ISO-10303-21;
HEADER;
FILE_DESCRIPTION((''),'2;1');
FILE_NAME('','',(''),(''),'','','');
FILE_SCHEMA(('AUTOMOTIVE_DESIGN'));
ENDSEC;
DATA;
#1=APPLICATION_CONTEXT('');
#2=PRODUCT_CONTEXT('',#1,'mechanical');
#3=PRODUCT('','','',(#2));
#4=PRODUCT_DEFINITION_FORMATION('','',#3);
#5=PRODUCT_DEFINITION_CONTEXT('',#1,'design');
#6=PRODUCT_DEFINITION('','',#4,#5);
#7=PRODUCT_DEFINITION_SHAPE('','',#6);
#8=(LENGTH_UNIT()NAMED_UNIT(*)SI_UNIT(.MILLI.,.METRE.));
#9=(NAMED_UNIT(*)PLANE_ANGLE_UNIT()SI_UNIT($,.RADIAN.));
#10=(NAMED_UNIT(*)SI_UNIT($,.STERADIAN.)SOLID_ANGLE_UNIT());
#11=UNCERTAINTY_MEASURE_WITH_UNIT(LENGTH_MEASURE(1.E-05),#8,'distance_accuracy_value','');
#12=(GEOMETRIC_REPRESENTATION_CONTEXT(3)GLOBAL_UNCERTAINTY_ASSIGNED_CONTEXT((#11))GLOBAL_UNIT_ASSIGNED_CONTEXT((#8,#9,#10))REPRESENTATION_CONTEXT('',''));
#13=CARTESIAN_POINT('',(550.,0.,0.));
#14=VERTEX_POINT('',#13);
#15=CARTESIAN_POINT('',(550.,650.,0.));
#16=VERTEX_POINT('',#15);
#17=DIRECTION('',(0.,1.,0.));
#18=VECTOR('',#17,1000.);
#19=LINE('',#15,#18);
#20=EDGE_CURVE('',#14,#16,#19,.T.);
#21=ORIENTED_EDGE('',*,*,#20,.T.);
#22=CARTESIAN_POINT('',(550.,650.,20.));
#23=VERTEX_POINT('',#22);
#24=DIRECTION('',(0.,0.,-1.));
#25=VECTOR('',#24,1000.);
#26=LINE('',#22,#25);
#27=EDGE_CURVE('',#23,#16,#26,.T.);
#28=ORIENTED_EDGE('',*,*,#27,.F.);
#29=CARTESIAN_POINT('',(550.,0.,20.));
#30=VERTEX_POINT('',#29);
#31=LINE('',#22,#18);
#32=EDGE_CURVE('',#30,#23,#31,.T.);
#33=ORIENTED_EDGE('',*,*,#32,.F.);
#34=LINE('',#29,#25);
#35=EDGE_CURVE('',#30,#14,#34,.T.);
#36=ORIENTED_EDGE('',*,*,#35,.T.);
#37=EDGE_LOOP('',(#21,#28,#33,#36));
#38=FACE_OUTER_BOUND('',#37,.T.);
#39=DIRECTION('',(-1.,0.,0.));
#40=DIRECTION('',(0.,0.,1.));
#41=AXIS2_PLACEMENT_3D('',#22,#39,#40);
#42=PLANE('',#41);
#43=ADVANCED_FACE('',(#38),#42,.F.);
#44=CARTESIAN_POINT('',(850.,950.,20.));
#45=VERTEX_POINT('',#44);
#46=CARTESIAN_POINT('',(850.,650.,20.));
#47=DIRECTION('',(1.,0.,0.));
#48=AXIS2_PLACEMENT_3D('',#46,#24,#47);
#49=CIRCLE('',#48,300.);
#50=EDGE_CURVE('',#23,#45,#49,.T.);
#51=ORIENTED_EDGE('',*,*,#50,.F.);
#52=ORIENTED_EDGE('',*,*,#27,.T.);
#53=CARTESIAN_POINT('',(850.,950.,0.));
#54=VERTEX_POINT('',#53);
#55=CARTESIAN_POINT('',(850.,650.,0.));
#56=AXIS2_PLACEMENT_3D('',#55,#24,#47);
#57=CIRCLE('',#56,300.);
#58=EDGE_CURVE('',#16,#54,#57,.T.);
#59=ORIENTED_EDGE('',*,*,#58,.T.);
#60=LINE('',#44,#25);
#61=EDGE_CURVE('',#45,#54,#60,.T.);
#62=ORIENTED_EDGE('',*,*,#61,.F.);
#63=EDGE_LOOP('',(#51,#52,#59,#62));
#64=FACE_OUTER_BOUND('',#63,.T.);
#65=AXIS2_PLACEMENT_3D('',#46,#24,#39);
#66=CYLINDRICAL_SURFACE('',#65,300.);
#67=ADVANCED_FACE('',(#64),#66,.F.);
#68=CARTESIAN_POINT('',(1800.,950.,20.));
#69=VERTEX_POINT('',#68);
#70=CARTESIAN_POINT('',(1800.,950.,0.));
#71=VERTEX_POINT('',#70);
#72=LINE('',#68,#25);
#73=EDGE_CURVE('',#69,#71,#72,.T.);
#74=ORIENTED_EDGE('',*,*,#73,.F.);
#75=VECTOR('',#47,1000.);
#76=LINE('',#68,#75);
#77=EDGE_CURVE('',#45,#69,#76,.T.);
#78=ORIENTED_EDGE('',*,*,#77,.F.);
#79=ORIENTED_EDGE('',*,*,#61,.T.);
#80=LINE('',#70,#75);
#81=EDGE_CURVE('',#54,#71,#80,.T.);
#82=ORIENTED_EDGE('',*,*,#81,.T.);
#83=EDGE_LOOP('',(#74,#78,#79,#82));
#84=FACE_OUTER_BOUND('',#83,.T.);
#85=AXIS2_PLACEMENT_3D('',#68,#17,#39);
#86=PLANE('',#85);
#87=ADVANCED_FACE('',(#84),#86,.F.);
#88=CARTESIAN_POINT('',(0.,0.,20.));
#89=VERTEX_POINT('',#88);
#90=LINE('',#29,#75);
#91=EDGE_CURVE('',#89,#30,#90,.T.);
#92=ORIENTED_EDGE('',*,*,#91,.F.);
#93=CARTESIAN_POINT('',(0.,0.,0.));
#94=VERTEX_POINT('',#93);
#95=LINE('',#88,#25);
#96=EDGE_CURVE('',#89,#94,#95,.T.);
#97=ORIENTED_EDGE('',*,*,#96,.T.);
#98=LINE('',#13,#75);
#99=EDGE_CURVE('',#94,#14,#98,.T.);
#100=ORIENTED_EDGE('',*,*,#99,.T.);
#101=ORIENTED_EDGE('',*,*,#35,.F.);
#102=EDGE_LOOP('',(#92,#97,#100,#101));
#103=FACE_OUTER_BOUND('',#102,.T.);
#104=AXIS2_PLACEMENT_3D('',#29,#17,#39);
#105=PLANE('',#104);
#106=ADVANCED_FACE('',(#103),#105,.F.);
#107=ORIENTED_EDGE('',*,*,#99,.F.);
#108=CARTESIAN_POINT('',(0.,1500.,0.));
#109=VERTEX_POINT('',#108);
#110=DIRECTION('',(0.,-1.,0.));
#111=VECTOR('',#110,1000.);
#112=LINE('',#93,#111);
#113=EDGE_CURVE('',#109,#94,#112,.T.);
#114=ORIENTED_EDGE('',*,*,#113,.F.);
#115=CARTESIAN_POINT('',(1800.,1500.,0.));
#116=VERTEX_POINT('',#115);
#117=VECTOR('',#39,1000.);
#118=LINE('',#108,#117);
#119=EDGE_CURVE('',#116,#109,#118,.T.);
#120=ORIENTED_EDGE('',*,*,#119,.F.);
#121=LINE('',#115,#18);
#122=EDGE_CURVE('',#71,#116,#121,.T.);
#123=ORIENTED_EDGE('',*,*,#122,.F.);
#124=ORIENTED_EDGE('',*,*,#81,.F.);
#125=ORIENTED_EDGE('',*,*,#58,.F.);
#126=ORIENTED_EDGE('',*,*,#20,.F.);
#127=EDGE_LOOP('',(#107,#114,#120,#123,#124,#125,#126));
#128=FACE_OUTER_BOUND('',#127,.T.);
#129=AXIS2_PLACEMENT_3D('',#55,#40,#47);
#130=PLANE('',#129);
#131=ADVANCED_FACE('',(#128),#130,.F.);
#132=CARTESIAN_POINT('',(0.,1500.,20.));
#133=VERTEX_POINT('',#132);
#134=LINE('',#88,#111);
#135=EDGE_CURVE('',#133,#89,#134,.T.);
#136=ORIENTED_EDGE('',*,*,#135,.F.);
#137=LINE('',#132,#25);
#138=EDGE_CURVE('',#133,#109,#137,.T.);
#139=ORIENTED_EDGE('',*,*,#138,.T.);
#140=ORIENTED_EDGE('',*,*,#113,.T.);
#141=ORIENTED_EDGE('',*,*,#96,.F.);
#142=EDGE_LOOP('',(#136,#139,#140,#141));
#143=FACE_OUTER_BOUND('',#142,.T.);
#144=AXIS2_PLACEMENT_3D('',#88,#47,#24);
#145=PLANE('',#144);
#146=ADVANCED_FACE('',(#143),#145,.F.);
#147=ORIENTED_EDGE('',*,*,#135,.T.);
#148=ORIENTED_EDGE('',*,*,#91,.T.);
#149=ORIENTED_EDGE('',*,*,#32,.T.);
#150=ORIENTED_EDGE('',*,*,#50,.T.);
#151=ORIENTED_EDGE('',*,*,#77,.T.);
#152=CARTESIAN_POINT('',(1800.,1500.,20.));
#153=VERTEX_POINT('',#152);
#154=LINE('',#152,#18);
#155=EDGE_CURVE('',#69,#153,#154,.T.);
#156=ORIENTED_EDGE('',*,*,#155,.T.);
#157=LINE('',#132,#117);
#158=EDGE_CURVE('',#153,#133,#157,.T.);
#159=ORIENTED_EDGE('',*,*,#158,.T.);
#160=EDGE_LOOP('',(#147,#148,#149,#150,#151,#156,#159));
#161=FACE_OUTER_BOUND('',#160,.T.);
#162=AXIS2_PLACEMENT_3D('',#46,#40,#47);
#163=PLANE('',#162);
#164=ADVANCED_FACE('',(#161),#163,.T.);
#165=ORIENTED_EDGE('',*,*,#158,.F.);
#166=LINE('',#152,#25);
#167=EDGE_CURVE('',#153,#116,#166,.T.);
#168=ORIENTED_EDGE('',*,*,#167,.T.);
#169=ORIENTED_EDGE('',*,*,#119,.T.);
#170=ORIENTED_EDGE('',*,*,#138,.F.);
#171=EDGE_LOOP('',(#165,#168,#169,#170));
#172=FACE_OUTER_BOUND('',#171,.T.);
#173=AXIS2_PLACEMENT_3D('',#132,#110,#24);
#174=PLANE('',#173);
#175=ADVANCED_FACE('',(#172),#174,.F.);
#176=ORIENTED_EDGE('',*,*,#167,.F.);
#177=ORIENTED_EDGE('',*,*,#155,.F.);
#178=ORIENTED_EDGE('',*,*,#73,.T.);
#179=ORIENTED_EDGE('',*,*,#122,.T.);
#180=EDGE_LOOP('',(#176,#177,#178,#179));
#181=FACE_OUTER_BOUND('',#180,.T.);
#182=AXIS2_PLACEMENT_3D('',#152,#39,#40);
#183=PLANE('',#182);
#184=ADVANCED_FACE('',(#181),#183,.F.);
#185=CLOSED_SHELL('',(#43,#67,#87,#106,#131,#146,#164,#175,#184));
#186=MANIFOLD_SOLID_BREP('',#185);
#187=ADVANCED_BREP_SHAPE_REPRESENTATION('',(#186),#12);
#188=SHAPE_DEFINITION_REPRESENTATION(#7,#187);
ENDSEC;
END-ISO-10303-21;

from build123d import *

# Parameters (mm, degrees)
BOSS_EXTRUDE1_DEPTH = 20


with BuildPart() as part:
    # Sketch1 → Boss-Extrude1 (new body)
    with BuildSketch(Plane.XY):
        with BuildLine():
            Line((0, 0), (0, 1500))
            Line((0, 1500), (1800, 1500))
            Line((1800, 1500), (1800, 950))
            Line((1800, 950), (850, 950))
            ThreePointArc((850, 950), (637.867965644, 862.132034356), (550, 650))
            Line((550, 650), (550, 0))
            Line((550, 0), (0, 0))
        make_face()
    extrude(amount=BOSS_EXTRUDE1_DEPTH)


solid = part.part
